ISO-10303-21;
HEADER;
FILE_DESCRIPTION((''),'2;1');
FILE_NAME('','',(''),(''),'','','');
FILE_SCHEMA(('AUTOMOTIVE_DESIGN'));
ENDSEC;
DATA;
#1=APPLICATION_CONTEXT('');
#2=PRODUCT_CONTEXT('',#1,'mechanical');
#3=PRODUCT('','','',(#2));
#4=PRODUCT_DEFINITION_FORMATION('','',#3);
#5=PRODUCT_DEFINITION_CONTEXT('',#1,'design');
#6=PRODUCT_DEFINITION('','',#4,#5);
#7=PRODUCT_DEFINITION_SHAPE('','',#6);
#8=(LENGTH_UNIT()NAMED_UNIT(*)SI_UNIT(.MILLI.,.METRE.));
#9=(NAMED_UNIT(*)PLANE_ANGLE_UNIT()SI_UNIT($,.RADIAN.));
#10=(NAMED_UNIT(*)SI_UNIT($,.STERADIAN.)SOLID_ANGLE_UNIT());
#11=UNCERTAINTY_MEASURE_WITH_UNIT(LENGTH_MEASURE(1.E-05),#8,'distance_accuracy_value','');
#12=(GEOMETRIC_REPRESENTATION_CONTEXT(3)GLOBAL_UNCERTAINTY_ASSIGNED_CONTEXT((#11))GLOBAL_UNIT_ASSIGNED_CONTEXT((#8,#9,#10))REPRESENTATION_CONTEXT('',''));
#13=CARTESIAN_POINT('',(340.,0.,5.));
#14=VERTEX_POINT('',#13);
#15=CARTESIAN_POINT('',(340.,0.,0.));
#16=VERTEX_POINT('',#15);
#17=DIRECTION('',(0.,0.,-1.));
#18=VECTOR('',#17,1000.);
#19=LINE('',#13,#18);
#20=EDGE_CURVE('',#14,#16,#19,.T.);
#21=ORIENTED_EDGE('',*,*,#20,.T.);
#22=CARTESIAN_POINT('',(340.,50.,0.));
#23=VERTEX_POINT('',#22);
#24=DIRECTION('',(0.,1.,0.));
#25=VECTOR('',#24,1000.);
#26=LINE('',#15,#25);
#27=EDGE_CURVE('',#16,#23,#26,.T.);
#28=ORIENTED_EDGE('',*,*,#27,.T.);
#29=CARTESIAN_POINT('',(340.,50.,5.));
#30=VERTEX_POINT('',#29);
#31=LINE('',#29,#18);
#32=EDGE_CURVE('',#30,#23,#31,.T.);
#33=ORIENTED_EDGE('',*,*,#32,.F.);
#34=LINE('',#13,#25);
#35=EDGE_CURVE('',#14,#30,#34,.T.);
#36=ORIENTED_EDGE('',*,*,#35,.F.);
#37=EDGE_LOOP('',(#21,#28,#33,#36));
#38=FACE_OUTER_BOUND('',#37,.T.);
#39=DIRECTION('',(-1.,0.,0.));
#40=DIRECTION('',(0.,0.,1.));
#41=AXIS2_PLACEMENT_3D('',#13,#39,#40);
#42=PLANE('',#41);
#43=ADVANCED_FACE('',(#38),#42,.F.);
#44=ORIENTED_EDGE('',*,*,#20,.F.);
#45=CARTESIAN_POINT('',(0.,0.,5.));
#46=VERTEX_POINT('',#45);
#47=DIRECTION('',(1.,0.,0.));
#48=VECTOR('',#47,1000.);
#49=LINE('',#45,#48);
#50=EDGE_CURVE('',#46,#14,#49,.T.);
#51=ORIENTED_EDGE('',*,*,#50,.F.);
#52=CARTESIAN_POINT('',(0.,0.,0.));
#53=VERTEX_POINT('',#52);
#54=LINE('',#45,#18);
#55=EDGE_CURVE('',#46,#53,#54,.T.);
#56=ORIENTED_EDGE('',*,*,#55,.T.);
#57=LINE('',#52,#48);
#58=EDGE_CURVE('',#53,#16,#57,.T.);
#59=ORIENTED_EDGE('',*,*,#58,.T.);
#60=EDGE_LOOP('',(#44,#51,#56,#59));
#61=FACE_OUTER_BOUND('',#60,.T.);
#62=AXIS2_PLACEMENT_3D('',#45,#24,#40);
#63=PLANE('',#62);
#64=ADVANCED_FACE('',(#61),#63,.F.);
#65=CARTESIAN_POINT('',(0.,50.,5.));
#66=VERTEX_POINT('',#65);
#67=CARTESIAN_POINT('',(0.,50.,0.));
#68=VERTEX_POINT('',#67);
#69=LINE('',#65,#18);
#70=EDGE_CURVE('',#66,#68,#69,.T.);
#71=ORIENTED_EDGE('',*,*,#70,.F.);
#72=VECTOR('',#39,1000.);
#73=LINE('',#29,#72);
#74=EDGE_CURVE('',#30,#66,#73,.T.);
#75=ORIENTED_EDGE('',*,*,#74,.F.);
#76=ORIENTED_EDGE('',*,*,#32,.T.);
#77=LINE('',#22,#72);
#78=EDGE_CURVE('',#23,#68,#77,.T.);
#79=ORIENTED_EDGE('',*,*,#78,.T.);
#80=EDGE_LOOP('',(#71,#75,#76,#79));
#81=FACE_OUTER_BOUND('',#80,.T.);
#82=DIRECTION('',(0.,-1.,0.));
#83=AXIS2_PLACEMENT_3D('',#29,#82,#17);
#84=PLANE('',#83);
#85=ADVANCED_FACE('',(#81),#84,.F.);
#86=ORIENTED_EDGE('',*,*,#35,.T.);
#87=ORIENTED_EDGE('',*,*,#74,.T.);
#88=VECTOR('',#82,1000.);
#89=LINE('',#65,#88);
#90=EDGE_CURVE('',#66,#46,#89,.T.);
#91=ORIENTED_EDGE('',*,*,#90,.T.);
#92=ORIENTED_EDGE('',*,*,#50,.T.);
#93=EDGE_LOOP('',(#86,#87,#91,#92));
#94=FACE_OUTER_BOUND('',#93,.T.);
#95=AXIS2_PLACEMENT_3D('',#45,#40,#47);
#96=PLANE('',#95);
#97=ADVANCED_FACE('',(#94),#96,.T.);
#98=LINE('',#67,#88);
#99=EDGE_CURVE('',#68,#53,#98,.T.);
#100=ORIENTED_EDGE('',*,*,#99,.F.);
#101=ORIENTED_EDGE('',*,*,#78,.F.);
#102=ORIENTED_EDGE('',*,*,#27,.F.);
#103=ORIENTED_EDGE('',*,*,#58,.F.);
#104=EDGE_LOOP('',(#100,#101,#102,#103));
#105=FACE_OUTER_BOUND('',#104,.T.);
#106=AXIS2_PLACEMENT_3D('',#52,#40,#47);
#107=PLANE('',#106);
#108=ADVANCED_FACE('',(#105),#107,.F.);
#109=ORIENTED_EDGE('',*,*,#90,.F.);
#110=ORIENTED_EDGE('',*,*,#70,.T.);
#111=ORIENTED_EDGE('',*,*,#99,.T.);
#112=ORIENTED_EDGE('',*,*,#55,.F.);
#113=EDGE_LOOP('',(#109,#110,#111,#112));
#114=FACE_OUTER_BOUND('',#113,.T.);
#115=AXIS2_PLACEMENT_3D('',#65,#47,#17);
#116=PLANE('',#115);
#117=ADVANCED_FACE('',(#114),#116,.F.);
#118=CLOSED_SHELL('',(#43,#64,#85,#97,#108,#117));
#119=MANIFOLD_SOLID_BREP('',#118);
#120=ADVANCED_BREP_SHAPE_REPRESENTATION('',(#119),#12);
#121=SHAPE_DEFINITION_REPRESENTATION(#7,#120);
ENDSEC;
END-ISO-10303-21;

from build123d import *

# Parameters (mm, degrees)
SKETCH_1_W      = 340
SKETCH_1_H      = 50
EXTRUDE_1_DEPTH = 5


with BuildPart() as part:
    # 草图1 → 凸台-拉伸1 (new body)
    with BuildSketch(Plane.XY):
        with Locations((170, 25)):
            Rectangle(SKETCH_1_W, SKETCH_1_H)
    extrude(amount=EXTRUDE_1_DEPTH)


solid = part.part
